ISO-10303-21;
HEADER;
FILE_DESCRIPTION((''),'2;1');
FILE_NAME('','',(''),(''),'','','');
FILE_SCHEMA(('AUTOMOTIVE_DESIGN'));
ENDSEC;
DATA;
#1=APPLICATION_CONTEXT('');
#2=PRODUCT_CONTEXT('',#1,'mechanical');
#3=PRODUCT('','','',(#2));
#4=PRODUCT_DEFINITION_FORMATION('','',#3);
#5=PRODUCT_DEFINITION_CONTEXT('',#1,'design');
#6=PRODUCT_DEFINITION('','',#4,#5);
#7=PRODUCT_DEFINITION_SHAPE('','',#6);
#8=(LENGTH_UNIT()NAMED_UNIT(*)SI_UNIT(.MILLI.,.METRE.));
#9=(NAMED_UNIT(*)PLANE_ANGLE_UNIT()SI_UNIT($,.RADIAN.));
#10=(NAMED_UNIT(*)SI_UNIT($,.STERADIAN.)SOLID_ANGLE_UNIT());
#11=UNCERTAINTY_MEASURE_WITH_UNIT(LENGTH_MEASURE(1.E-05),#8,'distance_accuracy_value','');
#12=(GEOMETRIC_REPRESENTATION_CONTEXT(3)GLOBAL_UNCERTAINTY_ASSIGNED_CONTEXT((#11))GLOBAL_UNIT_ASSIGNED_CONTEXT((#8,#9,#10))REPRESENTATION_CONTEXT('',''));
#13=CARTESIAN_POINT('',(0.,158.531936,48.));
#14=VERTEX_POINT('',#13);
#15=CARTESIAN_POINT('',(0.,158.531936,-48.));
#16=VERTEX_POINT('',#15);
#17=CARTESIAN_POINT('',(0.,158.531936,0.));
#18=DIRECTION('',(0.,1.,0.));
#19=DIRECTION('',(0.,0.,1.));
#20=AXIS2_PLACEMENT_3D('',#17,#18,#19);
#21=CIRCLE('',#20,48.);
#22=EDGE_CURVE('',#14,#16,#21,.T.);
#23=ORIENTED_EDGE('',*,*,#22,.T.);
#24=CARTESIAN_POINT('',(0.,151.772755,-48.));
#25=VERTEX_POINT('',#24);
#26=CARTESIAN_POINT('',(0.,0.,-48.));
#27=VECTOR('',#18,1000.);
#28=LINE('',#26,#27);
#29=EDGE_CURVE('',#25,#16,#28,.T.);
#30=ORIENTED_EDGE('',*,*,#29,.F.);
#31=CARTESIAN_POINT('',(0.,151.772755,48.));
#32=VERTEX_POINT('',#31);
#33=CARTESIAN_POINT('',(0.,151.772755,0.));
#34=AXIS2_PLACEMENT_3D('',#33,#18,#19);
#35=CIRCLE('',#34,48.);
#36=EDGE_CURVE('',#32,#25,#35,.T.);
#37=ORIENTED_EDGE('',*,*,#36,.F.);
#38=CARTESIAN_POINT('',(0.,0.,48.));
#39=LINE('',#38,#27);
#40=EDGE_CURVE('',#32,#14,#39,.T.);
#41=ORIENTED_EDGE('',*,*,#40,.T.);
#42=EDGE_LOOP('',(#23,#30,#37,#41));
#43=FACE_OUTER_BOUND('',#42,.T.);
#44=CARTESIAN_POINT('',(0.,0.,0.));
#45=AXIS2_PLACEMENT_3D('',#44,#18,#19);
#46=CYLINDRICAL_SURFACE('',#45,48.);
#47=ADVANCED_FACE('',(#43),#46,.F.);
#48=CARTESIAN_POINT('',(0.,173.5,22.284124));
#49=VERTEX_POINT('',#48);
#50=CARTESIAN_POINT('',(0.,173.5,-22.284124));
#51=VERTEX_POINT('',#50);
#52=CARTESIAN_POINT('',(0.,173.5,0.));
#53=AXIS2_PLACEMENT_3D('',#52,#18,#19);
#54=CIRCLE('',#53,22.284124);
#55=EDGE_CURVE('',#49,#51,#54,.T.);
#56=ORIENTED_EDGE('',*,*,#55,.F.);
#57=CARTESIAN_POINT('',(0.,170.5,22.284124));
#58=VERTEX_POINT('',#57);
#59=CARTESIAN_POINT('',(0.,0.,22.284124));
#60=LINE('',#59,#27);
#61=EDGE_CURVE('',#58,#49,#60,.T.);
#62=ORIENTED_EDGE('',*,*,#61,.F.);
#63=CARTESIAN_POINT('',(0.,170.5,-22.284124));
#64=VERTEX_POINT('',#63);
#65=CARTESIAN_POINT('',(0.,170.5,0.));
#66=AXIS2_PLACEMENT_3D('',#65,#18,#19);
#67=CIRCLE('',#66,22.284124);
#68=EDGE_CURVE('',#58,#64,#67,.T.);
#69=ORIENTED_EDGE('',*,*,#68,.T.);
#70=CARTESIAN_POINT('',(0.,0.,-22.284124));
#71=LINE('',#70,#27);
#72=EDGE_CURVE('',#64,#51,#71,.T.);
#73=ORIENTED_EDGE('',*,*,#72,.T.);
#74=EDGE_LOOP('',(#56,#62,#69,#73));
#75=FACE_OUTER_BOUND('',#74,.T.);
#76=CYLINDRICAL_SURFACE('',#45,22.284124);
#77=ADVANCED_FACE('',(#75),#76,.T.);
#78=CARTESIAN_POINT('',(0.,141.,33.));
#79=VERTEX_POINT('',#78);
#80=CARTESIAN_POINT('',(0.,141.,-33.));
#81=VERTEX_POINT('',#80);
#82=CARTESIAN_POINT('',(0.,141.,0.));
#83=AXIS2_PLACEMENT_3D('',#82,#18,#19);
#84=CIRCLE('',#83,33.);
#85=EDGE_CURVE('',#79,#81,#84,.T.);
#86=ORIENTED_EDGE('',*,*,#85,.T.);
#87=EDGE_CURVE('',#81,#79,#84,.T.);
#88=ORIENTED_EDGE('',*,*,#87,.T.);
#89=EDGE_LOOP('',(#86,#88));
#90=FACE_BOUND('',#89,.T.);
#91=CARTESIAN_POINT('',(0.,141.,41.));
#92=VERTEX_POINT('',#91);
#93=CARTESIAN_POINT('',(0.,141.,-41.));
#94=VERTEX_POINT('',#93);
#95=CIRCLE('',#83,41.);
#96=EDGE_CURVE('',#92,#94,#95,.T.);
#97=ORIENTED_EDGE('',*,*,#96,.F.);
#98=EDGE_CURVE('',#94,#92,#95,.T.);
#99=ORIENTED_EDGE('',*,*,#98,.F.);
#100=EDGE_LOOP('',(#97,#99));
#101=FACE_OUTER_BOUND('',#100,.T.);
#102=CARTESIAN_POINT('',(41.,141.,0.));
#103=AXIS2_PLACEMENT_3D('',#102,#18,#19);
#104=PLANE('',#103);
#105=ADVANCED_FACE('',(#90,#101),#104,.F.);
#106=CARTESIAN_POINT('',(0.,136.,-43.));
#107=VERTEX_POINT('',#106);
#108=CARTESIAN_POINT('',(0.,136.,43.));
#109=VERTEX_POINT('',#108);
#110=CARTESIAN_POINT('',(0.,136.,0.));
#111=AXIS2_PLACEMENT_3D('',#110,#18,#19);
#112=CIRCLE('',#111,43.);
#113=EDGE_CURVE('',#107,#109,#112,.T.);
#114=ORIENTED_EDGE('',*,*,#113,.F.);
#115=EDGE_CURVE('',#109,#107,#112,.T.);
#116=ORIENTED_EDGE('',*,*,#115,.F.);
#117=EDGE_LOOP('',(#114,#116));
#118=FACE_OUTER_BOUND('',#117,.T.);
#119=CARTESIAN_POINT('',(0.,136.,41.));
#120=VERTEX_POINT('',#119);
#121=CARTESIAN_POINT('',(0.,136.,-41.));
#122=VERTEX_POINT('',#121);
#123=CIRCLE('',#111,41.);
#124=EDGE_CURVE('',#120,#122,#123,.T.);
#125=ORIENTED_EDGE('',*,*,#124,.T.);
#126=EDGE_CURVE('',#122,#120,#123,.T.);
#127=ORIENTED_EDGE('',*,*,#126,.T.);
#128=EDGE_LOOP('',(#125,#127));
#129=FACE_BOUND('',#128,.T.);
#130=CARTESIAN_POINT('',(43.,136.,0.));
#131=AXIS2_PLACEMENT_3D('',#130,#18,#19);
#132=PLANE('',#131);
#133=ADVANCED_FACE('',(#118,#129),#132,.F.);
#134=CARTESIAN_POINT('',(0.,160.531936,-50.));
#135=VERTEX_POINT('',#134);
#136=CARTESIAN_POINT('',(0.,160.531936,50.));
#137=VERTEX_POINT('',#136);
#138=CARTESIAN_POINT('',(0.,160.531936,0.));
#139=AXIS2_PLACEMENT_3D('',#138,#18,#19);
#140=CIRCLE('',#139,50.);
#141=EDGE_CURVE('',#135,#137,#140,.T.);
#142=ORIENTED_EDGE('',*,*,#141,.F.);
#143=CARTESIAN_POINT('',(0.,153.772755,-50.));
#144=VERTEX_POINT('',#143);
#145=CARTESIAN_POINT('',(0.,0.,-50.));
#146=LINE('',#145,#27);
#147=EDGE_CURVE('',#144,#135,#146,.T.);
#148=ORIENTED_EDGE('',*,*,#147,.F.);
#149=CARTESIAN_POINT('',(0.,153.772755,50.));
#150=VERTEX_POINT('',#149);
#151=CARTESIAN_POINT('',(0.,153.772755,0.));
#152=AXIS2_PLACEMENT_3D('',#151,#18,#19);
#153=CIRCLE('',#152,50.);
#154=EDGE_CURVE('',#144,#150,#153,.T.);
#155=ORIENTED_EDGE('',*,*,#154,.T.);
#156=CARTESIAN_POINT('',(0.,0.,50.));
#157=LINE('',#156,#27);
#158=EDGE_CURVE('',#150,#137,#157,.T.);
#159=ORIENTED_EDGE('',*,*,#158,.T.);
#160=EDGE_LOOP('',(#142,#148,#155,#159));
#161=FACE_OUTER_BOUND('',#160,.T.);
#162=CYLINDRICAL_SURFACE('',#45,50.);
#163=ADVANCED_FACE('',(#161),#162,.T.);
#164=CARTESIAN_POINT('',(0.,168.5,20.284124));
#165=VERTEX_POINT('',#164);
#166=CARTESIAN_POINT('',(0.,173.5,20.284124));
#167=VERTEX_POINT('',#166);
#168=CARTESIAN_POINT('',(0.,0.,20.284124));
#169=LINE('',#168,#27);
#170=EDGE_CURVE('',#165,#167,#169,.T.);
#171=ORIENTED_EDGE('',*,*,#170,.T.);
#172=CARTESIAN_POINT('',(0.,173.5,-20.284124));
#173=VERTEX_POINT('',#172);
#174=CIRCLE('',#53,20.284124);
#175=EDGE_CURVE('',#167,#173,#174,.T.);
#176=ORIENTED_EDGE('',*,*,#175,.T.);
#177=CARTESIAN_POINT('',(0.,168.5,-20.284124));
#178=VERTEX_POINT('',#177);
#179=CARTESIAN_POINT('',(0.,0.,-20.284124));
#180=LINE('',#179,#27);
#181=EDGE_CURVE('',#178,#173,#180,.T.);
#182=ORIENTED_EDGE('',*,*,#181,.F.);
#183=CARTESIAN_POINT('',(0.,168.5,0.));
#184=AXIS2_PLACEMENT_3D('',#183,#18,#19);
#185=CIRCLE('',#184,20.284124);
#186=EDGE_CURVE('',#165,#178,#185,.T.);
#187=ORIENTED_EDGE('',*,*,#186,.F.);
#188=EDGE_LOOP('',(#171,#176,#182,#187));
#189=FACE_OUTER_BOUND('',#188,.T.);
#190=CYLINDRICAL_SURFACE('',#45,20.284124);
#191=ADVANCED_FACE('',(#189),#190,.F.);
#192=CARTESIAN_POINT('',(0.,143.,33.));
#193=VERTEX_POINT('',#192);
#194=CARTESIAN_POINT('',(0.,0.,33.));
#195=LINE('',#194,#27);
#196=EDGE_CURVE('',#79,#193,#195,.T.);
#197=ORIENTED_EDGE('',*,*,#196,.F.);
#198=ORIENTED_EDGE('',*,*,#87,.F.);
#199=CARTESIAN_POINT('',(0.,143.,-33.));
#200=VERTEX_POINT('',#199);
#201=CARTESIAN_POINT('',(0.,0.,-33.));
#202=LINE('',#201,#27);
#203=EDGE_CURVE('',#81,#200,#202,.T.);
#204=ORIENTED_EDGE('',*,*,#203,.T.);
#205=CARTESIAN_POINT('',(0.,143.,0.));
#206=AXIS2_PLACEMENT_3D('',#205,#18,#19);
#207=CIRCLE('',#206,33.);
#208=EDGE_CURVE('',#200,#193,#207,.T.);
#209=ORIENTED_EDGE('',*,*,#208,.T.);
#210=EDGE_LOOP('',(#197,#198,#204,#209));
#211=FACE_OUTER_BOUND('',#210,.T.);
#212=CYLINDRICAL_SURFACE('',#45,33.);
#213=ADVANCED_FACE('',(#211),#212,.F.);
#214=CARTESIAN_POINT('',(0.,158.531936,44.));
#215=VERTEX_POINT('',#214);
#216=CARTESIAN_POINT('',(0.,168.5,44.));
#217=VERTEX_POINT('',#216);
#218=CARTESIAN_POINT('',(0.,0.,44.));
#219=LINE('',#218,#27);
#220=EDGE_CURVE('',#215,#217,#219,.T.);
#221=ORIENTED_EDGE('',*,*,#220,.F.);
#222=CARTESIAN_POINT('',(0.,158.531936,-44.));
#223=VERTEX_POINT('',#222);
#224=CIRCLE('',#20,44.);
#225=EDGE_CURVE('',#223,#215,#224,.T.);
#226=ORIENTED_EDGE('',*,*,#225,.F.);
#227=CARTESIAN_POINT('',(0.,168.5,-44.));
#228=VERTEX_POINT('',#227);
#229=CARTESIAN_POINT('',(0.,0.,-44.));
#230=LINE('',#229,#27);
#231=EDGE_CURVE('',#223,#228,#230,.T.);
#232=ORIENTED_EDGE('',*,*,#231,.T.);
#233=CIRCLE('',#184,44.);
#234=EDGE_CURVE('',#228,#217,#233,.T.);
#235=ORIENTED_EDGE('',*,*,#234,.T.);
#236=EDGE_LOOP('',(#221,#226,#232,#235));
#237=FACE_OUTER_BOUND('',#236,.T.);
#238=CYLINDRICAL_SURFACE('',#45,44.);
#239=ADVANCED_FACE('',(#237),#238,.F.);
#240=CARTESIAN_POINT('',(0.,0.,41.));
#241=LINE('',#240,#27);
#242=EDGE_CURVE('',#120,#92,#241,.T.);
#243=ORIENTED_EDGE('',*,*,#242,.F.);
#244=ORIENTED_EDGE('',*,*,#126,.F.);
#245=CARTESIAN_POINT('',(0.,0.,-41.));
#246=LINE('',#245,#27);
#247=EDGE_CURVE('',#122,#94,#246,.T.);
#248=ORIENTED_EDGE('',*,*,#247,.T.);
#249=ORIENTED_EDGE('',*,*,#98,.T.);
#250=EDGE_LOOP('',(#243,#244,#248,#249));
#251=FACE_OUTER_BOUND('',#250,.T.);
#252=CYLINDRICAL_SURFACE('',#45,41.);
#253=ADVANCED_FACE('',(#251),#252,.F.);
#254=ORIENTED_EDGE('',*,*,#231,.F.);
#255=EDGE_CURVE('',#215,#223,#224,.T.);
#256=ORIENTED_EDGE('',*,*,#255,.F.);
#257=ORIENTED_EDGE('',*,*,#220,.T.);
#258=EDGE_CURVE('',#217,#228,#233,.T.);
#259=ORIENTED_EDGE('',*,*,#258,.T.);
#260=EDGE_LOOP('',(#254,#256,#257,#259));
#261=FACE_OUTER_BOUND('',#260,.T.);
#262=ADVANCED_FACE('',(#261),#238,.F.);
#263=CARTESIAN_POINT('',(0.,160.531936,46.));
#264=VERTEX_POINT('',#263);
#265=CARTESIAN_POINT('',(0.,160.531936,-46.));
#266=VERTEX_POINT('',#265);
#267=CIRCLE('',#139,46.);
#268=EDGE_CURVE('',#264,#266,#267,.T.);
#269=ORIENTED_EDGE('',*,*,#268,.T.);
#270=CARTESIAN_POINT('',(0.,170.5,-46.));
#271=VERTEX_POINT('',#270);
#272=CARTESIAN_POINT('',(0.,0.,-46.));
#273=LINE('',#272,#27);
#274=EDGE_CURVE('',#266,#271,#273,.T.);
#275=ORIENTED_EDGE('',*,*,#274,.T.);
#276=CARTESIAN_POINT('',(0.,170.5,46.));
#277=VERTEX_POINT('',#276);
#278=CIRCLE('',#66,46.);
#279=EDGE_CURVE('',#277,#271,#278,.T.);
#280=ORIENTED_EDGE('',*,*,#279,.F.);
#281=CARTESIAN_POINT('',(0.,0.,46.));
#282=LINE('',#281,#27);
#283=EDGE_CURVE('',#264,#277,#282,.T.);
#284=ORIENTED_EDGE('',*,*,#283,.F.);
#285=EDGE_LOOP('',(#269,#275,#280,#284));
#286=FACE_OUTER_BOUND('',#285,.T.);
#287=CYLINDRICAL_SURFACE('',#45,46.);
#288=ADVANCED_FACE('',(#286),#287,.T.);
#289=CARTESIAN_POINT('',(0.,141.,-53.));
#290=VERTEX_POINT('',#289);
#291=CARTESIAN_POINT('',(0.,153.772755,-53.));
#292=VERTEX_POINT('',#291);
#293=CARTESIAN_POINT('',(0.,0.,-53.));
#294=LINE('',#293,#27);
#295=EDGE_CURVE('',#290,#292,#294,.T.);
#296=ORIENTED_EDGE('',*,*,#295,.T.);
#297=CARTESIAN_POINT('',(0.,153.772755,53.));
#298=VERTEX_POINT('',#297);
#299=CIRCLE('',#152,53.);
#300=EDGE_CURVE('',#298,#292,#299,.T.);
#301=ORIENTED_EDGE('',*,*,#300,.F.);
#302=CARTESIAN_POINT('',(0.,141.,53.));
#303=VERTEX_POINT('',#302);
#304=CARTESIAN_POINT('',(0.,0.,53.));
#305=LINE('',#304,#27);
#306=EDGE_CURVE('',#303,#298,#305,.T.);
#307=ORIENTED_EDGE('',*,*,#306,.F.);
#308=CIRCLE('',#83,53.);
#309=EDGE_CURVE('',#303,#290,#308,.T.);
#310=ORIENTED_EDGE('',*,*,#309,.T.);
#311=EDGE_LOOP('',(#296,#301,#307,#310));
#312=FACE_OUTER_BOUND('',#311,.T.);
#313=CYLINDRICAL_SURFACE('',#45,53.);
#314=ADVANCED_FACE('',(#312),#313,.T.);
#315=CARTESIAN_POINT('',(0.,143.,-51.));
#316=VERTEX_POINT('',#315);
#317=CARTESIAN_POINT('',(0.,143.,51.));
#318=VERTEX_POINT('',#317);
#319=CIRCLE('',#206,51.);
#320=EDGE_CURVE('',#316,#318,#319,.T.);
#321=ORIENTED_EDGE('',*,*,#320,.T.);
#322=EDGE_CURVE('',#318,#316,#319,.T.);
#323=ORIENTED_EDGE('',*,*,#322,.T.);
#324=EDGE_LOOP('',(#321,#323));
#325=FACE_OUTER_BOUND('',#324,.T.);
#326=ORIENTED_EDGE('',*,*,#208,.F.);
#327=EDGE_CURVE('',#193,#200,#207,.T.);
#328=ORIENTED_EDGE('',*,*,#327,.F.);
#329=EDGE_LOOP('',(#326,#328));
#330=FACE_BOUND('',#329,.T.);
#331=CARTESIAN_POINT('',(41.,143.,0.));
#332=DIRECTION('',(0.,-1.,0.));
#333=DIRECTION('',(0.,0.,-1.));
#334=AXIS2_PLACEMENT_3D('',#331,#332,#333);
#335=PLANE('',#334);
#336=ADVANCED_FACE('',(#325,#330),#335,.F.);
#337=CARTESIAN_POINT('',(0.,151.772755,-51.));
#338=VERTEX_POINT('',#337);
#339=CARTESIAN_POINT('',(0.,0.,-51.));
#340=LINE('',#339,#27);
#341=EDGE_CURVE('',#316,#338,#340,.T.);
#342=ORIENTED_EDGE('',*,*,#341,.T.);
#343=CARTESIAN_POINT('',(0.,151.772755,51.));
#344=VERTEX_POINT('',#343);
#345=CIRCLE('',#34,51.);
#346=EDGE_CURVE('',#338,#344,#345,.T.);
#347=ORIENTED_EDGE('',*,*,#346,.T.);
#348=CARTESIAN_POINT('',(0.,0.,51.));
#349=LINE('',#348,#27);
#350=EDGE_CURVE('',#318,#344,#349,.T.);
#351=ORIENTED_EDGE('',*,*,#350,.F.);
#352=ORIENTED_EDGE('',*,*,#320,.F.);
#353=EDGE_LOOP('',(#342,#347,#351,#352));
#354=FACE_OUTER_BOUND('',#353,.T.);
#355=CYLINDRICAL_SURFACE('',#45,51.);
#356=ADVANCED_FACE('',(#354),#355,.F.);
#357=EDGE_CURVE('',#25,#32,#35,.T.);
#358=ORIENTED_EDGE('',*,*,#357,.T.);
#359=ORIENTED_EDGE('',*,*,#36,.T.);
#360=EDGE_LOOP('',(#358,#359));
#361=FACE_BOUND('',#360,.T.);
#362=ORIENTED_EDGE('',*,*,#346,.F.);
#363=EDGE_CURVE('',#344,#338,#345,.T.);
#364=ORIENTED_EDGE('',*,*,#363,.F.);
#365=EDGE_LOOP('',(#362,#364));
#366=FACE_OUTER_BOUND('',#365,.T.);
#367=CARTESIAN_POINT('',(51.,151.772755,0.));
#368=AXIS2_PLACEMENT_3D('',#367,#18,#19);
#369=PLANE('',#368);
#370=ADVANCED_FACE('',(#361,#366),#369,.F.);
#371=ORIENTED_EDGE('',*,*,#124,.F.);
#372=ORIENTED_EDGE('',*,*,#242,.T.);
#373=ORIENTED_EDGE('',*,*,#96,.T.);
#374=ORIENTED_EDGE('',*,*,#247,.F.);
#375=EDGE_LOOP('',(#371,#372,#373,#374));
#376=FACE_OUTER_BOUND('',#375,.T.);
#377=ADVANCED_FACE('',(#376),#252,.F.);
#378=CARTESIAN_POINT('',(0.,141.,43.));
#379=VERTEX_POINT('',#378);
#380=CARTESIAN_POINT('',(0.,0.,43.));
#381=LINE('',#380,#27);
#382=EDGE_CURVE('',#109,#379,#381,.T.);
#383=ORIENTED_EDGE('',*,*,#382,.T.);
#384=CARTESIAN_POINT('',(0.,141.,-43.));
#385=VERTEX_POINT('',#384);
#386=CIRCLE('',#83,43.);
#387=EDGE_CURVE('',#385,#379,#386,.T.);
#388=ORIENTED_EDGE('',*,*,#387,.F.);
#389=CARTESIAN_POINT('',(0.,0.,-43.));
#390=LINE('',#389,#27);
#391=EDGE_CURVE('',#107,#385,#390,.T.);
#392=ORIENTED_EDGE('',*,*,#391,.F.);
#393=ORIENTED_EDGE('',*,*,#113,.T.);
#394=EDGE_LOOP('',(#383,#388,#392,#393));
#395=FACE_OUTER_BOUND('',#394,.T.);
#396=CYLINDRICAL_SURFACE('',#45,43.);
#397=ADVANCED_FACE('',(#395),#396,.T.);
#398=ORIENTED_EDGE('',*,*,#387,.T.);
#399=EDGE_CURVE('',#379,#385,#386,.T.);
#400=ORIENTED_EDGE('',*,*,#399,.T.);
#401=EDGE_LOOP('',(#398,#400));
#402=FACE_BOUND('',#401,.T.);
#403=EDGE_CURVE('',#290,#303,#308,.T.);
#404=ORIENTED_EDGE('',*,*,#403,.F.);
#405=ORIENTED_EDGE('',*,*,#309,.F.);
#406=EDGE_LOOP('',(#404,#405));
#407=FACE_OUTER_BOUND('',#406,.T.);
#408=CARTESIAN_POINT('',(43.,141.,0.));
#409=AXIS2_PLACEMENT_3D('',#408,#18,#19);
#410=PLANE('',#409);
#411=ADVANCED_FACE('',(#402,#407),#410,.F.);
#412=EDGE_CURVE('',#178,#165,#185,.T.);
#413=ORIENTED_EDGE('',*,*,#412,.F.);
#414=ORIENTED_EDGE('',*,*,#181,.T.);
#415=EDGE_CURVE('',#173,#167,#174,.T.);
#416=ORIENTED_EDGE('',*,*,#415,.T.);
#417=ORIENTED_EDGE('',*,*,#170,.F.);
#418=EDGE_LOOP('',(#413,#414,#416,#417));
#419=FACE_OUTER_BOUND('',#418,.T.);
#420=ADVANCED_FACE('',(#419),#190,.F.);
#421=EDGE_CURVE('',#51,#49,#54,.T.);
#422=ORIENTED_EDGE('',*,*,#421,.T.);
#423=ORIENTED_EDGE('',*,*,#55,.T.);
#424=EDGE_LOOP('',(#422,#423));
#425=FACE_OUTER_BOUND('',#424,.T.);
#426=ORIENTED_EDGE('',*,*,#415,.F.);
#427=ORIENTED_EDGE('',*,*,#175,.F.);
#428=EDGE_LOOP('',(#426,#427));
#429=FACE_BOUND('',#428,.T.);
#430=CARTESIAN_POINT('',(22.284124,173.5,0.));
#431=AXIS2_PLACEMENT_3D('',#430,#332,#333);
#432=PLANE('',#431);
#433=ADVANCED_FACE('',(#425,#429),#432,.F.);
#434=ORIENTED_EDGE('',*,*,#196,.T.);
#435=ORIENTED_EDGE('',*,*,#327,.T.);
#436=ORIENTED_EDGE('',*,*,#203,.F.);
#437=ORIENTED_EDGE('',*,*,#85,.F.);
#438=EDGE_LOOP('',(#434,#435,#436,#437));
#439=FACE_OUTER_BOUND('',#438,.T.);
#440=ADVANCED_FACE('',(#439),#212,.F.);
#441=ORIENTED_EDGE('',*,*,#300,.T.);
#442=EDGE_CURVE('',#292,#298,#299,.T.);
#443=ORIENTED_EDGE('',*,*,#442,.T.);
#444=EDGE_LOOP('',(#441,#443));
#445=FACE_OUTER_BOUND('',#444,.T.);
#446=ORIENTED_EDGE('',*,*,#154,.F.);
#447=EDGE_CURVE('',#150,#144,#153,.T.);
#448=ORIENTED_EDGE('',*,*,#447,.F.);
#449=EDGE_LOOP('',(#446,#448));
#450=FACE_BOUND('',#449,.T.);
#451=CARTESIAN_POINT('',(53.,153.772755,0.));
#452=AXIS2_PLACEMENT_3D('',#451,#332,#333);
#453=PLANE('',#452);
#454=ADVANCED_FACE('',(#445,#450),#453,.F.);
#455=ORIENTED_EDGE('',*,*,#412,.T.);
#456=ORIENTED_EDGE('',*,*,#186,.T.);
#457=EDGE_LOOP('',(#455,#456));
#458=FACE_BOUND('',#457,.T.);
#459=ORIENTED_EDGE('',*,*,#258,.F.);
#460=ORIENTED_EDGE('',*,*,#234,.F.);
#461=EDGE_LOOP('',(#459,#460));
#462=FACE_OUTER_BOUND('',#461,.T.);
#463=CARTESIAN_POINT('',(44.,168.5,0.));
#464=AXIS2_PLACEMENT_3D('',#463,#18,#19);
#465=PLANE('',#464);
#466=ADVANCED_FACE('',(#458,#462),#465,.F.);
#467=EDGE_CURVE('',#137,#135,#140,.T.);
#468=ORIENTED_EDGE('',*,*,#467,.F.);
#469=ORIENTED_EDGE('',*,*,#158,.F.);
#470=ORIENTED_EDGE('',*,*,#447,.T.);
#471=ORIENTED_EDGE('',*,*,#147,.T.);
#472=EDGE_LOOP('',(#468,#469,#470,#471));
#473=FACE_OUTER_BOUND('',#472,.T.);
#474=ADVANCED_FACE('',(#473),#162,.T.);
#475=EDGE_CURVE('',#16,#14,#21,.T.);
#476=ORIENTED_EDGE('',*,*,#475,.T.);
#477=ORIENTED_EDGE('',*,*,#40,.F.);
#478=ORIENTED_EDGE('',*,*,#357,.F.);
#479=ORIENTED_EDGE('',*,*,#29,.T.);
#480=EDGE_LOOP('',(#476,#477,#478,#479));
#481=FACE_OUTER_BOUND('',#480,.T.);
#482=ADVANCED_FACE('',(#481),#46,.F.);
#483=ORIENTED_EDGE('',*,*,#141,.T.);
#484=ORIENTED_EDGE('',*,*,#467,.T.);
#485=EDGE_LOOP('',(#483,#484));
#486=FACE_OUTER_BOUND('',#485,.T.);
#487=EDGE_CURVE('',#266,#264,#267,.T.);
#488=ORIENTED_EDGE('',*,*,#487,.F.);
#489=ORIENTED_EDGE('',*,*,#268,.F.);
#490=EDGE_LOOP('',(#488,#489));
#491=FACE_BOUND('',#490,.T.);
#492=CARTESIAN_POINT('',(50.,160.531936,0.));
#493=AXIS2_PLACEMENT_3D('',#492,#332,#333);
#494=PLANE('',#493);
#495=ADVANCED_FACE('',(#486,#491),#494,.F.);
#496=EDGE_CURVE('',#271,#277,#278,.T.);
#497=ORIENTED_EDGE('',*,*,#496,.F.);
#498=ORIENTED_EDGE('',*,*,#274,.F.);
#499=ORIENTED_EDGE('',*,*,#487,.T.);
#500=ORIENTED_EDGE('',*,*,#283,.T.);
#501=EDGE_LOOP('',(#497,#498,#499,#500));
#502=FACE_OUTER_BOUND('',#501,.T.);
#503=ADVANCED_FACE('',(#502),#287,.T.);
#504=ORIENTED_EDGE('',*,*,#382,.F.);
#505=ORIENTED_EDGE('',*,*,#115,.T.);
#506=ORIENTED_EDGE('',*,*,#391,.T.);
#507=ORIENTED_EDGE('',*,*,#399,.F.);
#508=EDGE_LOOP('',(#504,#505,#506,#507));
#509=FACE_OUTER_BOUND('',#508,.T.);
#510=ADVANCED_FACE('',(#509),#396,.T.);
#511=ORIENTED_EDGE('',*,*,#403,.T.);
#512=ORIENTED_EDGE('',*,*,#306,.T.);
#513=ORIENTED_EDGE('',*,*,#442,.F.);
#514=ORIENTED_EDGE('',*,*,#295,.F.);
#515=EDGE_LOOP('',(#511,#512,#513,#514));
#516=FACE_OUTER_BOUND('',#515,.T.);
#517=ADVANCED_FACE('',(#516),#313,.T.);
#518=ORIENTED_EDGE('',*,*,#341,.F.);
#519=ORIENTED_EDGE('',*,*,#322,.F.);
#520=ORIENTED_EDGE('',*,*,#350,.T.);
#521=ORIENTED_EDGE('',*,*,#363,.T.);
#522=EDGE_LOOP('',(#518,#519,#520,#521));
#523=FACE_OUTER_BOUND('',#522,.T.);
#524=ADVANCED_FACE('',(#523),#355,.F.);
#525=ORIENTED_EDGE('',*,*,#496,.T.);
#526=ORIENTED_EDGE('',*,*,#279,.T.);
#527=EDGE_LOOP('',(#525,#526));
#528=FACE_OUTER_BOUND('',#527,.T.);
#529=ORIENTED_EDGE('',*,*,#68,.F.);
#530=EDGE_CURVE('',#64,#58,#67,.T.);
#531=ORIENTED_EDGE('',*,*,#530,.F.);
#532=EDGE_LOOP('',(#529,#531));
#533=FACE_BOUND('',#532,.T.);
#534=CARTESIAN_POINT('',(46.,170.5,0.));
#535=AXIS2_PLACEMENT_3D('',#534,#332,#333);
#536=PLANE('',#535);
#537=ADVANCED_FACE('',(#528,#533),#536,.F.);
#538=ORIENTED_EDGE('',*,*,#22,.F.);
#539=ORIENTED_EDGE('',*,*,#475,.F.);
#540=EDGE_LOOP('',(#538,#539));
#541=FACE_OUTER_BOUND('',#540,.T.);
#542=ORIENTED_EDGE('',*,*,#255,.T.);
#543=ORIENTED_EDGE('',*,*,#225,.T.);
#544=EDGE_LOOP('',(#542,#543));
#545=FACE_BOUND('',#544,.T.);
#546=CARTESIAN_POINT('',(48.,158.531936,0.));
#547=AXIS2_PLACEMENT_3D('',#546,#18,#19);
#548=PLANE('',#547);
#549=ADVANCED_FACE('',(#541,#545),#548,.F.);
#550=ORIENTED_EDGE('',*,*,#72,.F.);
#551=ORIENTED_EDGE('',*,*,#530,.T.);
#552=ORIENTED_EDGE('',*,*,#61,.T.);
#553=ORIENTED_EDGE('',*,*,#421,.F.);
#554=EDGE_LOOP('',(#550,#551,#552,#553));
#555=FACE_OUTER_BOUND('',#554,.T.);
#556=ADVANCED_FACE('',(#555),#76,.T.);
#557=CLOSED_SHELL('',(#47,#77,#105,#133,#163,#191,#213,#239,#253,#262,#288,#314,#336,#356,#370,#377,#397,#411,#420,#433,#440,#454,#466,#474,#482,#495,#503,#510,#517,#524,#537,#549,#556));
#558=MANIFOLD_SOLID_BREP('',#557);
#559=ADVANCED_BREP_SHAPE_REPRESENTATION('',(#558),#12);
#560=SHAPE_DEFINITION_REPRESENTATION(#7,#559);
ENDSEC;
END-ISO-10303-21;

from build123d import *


with BuildPart() as part:
    # Sketch1 → Revolve1 (revolve)
    with BuildSketch(Plane.XY, mode=Mode.PRIVATE) as revolve1_sk:
        Polygon((43, 136), (43, 141), (53, 141), (53, 153.772755302), (50, 153.772755302), (50, 160.531936258), (46, 160.531936258), (46, 170.5), (22.284123589, 170.5), (22.284123589, 173.5), (20.284123589, 173.5), (20.284123589, 168.5), (44, 168.5), (44, 158.531936258), (48, 158.531936258), (48, 151.772755302), (51, 151.772755302), (51, 143), (41, 143), (33, 143), (33, 141), (41, 141), (41, 136), align=None)
    revolve(revolve1_sk.sketch.rotate(Axis((0, 0, 0), (0, -1, 0)), 90), axis=Axis((0, 0, 0), (0, -1, 0)))


solid = part.part
